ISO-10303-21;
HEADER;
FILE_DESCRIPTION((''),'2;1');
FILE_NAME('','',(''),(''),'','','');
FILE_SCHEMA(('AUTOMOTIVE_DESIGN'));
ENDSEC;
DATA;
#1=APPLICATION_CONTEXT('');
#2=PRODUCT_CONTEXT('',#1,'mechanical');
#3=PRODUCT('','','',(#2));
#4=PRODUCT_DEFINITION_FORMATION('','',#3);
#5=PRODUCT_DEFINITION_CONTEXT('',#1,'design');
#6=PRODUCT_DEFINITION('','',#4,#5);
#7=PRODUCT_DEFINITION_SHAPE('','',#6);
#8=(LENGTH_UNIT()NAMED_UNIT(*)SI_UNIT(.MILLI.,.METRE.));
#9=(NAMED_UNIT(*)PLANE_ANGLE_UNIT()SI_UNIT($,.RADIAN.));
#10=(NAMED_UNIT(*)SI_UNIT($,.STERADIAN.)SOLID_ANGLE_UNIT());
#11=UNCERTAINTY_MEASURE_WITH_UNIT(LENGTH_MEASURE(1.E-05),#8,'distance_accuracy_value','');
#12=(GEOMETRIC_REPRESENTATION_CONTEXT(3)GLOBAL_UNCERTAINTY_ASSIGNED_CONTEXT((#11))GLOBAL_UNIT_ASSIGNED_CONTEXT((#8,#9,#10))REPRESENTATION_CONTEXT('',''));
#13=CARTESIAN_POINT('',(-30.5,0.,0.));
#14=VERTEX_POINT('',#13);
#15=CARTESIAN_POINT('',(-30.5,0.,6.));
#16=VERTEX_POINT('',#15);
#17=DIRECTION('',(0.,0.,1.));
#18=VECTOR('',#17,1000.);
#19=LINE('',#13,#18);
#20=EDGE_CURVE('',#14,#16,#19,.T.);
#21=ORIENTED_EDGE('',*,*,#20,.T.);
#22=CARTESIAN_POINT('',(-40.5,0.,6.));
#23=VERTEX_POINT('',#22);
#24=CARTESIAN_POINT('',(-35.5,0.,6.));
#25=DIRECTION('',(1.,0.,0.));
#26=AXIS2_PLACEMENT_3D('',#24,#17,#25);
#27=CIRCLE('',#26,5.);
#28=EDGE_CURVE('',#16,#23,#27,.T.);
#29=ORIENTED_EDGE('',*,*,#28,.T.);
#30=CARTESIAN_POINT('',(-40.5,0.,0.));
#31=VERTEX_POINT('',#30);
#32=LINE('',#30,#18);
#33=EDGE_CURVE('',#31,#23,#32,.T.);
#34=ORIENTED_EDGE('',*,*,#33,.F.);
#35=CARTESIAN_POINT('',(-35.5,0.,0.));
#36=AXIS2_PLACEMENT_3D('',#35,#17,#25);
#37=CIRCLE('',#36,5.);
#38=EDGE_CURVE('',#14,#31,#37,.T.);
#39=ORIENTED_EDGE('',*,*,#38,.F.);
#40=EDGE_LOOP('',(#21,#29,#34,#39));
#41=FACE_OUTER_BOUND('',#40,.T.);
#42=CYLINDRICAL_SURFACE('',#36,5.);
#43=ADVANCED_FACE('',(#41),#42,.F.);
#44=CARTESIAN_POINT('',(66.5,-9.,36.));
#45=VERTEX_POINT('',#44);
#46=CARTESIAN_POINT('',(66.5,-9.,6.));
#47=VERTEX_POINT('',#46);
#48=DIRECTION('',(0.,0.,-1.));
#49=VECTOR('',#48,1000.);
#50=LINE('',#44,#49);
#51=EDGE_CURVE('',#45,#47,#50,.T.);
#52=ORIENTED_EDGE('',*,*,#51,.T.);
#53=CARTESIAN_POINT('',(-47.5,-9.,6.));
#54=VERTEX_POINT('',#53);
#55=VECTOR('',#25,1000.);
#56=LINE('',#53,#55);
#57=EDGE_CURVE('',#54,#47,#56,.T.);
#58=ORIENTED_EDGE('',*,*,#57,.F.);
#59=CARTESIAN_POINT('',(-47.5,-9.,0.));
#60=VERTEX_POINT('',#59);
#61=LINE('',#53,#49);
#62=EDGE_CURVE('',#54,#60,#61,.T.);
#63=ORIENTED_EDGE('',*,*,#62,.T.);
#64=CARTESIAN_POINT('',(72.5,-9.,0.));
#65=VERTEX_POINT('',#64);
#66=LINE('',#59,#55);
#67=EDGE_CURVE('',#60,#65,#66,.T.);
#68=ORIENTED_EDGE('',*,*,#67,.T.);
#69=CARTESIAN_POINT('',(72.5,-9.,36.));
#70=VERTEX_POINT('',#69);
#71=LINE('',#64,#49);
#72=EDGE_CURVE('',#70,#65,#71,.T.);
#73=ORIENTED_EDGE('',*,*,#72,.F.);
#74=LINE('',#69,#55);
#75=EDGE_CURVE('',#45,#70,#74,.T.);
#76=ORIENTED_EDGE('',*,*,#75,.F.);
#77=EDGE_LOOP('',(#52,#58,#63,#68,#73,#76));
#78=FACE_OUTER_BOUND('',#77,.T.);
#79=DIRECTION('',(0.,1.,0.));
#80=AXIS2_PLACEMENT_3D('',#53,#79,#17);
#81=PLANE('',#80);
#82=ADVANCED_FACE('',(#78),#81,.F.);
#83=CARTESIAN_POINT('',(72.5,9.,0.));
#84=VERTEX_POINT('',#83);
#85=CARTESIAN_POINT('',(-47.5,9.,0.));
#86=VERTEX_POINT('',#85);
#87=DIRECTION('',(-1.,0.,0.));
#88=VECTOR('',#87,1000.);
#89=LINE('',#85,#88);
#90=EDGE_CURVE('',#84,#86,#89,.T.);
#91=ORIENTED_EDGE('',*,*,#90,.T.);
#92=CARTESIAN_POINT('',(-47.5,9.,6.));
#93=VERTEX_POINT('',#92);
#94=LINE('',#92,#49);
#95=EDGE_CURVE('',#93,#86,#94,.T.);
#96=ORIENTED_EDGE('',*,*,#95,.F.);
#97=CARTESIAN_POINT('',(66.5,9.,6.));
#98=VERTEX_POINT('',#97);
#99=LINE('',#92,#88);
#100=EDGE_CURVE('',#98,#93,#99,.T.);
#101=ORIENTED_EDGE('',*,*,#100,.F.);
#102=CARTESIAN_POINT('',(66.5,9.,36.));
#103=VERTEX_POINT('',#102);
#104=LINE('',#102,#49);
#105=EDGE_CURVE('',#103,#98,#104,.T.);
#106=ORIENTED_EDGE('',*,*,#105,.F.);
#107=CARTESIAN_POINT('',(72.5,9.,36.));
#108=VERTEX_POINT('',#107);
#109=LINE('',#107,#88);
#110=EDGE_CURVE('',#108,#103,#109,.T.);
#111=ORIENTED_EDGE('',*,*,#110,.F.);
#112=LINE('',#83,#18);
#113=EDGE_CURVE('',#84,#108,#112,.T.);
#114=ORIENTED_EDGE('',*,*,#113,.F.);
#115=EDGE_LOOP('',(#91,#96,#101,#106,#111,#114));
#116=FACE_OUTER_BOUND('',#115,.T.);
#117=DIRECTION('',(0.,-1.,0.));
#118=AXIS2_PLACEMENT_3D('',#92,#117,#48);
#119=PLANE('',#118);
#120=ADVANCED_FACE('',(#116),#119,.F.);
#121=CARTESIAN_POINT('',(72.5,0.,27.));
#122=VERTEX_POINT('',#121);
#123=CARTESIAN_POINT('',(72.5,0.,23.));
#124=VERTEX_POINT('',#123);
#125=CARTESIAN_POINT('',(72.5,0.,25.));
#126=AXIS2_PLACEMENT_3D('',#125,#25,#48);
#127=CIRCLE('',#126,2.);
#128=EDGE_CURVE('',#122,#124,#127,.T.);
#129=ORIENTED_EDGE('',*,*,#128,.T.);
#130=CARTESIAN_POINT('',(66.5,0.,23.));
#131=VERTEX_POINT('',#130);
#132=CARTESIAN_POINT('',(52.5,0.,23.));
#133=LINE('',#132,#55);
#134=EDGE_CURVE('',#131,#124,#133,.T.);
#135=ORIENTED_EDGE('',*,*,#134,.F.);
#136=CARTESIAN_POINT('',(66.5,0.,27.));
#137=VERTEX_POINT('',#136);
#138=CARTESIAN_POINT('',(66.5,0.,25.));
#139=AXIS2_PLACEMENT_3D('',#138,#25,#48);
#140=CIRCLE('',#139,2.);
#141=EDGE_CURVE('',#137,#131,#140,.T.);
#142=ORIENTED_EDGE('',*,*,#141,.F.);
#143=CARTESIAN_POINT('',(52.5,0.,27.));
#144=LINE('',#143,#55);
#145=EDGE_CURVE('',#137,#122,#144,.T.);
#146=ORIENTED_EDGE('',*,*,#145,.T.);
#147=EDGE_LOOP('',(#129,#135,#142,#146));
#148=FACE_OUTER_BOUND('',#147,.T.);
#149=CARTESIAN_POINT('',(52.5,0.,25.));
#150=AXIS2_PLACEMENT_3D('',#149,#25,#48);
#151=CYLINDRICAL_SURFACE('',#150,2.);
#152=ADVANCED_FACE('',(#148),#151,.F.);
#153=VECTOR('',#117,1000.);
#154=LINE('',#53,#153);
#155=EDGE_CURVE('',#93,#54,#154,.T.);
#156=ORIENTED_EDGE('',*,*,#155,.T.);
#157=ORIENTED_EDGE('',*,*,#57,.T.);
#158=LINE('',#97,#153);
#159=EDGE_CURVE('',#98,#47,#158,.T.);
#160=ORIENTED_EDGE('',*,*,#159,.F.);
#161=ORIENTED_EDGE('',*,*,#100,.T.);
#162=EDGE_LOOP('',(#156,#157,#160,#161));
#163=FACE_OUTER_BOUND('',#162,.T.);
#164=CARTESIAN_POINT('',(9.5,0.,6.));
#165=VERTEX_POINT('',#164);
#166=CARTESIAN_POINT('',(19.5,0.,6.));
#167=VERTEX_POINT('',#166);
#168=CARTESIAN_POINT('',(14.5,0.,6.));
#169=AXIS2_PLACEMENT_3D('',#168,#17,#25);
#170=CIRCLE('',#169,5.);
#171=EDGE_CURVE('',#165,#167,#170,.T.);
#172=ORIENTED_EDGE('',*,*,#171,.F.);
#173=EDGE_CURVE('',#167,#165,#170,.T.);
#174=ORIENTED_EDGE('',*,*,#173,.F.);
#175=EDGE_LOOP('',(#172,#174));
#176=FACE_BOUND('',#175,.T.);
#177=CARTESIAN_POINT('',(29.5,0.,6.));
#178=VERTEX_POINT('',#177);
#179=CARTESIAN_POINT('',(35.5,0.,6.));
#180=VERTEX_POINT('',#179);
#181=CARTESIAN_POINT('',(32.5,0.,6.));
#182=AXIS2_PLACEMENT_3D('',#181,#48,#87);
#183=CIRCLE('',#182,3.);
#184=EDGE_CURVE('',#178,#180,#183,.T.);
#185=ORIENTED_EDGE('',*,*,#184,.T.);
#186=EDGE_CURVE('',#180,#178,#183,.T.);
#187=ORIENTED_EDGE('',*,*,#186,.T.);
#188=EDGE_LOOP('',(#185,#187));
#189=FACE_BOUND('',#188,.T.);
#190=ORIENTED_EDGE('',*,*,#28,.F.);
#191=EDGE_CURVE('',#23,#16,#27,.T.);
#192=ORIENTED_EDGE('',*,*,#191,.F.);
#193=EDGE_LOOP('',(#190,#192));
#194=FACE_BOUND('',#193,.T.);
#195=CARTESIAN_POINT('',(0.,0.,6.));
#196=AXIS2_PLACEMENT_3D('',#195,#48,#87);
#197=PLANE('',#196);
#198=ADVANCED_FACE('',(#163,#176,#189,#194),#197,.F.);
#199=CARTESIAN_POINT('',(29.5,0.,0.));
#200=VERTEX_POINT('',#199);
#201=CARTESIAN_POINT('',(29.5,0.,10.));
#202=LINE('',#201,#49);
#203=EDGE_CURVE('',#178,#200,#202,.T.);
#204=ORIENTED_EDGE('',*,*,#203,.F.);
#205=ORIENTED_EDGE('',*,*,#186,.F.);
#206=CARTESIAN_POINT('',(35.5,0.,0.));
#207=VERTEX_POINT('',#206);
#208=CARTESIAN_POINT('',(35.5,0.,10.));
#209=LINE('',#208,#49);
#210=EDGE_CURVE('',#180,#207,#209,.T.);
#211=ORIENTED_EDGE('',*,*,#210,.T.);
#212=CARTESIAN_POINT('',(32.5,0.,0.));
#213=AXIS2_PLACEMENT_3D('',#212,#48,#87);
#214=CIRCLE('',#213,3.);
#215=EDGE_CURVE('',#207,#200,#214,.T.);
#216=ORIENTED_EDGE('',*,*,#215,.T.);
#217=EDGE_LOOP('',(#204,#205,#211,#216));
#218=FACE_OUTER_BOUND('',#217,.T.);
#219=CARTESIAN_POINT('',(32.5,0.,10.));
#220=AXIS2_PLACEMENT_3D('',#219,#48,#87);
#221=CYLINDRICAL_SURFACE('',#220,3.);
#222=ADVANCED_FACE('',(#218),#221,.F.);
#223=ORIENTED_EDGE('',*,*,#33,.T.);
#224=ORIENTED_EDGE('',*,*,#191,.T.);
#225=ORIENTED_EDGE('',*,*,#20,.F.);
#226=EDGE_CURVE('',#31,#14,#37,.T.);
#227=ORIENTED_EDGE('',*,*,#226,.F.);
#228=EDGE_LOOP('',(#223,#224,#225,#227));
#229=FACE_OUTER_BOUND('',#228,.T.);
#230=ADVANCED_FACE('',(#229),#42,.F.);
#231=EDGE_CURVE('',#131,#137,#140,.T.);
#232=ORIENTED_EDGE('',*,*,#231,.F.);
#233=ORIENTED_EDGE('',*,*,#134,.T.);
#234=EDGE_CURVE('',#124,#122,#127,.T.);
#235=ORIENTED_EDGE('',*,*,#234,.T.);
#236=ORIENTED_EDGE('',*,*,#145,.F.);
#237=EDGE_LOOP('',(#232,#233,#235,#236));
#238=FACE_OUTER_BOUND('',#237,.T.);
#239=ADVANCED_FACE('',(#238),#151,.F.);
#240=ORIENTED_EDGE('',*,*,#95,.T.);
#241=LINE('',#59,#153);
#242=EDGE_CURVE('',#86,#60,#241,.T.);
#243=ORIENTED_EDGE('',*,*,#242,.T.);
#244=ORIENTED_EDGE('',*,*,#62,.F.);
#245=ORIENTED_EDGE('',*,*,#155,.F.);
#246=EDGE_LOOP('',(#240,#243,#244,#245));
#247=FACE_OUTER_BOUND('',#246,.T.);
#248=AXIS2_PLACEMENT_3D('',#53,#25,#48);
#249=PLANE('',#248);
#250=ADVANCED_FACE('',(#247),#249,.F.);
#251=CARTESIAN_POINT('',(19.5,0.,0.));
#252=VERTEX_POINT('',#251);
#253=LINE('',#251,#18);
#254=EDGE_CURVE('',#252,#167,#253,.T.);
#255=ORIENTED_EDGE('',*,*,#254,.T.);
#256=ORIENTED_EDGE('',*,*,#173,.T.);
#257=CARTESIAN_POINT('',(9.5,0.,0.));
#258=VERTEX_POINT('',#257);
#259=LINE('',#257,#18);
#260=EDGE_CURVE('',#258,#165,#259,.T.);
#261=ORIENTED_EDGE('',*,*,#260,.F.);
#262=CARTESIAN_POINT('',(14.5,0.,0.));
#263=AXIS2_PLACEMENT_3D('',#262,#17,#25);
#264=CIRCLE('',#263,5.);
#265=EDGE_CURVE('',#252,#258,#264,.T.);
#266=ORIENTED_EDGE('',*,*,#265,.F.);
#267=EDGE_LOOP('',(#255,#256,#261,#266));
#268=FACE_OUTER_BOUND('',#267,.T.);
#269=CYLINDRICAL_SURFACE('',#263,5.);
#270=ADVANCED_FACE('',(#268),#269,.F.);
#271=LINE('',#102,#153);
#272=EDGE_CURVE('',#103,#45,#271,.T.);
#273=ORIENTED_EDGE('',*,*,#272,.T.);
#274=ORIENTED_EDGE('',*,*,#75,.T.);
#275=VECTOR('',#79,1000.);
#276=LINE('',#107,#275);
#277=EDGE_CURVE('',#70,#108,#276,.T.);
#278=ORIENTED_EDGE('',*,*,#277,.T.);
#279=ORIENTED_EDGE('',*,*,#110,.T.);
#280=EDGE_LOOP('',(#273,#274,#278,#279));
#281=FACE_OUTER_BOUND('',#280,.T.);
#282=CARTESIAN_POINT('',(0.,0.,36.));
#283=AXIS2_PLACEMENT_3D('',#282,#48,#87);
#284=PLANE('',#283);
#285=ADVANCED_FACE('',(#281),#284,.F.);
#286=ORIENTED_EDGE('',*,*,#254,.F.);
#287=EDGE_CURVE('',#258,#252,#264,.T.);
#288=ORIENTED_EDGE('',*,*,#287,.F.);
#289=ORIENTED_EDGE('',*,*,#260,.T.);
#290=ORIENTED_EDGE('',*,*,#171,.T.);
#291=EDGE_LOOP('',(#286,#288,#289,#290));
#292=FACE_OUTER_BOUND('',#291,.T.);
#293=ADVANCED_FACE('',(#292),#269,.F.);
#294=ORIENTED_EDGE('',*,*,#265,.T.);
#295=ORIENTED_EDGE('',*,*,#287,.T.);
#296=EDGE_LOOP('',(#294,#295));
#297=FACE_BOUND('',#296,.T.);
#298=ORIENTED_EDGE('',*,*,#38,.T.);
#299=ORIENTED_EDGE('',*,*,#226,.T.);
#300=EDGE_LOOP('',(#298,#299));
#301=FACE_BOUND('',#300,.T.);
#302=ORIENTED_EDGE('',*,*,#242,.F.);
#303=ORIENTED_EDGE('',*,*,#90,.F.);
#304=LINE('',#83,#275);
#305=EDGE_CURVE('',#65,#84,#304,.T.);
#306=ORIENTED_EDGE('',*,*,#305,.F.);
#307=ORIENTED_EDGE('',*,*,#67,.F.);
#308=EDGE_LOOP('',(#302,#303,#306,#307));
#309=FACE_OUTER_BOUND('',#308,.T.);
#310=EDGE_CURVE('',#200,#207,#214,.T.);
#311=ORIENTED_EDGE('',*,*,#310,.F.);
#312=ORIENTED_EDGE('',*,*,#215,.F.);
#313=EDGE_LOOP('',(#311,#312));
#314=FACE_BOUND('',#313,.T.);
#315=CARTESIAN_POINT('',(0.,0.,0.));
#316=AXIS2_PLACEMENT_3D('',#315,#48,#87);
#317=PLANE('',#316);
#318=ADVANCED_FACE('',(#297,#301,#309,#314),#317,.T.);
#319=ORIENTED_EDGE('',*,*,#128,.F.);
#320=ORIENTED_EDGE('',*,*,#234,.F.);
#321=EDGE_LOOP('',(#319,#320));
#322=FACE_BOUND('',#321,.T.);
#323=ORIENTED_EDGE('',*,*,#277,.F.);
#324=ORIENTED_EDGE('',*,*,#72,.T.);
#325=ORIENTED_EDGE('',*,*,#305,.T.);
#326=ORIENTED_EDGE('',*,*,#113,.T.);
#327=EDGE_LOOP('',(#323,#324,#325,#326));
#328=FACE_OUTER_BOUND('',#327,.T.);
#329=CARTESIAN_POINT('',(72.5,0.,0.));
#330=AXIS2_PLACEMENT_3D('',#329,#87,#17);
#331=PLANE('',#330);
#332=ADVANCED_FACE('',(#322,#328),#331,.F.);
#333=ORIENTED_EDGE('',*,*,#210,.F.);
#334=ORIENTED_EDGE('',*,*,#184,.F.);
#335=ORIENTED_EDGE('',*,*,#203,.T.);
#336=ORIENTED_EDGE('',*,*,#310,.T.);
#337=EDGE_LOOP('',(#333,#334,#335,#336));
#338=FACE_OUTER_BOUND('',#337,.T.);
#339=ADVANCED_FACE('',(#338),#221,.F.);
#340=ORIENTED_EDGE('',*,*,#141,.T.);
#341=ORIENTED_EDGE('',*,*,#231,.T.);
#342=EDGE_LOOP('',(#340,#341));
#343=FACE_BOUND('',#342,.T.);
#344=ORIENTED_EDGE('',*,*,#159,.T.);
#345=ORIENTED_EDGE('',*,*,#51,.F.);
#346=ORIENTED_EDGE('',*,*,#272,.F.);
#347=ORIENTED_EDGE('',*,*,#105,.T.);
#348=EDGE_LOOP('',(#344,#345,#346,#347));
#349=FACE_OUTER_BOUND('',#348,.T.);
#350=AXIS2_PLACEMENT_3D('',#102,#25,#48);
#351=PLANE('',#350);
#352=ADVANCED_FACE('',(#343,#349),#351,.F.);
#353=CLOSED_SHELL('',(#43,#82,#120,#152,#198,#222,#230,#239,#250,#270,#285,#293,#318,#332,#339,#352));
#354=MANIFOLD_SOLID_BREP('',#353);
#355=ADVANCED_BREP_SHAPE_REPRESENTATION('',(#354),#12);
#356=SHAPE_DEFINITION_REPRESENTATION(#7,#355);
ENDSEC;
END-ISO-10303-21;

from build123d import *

# Parameters (mm, degrees)
SKETCH_1_W          = 95
SKETCH_1_H          = 18
EXTRUDE_1_DEPTH     = 6
SKETCH_2_R          = 5
CUT_EXTRUDE_1_DEPTH = 6
SKETCH_5_R          = 3
CUT_EXTRUDE_3_DEPTH = 10
SKETCH_6_W          = 6
SKETCH_6_H          = 18
EXTRUDE_3_DEPTH     = 25
SKETCH_7_W          = 6
SKETCH_7_H          = 18
EXTRUDE_4_DEPTH     = 30
SKETCH_8_R          = 2
CUT_EXTRUDE_4_DEPTH = 20


with BuildPart() as part:
    # 草图1 → 凸台-拉伸1 (new body)
    with BuildSketch(Plane.XY):
        Rectangle(SKETCH_1_W, SKETCH_1_H)
    extrude(amount=EXTRUDE_1_DEPTH)

    # 草图2 → 切除-拉伸1 (cut)
    with BuildSketch(Plane.XY.offset(6)):
        with Locations((-35.5, 0)):
            Circle(SKETCH_2_R)
        with Locations((14.5, 0)):
            Circle(SKETCH_2_R)
    extrude(amount=-CUT_EXTRUDE_1_DEPTH, mode=Mode.SUBTRACT)

    # 草图5 → 切除-拉伸3 (cut)
    with BuildSketch(Plane(origin=(0, 0, 0), x_dir=(-1, 0, 0), z_dir=(0, 0, -1))):
        with Locations((-32.5, 0)):
            Circle(SKETCH_5_R)
    extrude(amount=-CUT_EXTRUDE_3_DEPTH, mode=Mode.SUBTRACT)

    # 草图6 → 凸台-拉伸3 (add)
    with BuildSketch(Plane(origin=(47.5, 0, 0), x_dir=(0, 0, -1), z_dir=(1, 0, 0))):
        with Locations((-3, 0)):
            Rectangle(SKETCH_6_W, SKETCH_6_H)
    extrude(amount=EXTRUDE_3_DEPTH)

    # 草图7 → 凸台-拉伸4 (add)
    with BuildSketch(Plane.XY.offset(6)):
        with Locations((69.5, 0)):
            Rectangle(SKETCH_7_W, SKETCH_7_H)
    extrude(amount=EXTRUDE_4_DEPTH)

    # 草图8 → 切除-拉伸4 (cut)
    with BuildSketch(Plane(origin=(72.5, 0, 0), x_dir=(0, 0, -1), z_dir=(1, 0, 0))):
        with Locations((-25, 0)):
            Circle(SKETCH_8_R)
    extrude(amount=-CUT_EXTRUDE_4_DEPTH, mode=Mode.SUBTRACT)


solid = part.part
